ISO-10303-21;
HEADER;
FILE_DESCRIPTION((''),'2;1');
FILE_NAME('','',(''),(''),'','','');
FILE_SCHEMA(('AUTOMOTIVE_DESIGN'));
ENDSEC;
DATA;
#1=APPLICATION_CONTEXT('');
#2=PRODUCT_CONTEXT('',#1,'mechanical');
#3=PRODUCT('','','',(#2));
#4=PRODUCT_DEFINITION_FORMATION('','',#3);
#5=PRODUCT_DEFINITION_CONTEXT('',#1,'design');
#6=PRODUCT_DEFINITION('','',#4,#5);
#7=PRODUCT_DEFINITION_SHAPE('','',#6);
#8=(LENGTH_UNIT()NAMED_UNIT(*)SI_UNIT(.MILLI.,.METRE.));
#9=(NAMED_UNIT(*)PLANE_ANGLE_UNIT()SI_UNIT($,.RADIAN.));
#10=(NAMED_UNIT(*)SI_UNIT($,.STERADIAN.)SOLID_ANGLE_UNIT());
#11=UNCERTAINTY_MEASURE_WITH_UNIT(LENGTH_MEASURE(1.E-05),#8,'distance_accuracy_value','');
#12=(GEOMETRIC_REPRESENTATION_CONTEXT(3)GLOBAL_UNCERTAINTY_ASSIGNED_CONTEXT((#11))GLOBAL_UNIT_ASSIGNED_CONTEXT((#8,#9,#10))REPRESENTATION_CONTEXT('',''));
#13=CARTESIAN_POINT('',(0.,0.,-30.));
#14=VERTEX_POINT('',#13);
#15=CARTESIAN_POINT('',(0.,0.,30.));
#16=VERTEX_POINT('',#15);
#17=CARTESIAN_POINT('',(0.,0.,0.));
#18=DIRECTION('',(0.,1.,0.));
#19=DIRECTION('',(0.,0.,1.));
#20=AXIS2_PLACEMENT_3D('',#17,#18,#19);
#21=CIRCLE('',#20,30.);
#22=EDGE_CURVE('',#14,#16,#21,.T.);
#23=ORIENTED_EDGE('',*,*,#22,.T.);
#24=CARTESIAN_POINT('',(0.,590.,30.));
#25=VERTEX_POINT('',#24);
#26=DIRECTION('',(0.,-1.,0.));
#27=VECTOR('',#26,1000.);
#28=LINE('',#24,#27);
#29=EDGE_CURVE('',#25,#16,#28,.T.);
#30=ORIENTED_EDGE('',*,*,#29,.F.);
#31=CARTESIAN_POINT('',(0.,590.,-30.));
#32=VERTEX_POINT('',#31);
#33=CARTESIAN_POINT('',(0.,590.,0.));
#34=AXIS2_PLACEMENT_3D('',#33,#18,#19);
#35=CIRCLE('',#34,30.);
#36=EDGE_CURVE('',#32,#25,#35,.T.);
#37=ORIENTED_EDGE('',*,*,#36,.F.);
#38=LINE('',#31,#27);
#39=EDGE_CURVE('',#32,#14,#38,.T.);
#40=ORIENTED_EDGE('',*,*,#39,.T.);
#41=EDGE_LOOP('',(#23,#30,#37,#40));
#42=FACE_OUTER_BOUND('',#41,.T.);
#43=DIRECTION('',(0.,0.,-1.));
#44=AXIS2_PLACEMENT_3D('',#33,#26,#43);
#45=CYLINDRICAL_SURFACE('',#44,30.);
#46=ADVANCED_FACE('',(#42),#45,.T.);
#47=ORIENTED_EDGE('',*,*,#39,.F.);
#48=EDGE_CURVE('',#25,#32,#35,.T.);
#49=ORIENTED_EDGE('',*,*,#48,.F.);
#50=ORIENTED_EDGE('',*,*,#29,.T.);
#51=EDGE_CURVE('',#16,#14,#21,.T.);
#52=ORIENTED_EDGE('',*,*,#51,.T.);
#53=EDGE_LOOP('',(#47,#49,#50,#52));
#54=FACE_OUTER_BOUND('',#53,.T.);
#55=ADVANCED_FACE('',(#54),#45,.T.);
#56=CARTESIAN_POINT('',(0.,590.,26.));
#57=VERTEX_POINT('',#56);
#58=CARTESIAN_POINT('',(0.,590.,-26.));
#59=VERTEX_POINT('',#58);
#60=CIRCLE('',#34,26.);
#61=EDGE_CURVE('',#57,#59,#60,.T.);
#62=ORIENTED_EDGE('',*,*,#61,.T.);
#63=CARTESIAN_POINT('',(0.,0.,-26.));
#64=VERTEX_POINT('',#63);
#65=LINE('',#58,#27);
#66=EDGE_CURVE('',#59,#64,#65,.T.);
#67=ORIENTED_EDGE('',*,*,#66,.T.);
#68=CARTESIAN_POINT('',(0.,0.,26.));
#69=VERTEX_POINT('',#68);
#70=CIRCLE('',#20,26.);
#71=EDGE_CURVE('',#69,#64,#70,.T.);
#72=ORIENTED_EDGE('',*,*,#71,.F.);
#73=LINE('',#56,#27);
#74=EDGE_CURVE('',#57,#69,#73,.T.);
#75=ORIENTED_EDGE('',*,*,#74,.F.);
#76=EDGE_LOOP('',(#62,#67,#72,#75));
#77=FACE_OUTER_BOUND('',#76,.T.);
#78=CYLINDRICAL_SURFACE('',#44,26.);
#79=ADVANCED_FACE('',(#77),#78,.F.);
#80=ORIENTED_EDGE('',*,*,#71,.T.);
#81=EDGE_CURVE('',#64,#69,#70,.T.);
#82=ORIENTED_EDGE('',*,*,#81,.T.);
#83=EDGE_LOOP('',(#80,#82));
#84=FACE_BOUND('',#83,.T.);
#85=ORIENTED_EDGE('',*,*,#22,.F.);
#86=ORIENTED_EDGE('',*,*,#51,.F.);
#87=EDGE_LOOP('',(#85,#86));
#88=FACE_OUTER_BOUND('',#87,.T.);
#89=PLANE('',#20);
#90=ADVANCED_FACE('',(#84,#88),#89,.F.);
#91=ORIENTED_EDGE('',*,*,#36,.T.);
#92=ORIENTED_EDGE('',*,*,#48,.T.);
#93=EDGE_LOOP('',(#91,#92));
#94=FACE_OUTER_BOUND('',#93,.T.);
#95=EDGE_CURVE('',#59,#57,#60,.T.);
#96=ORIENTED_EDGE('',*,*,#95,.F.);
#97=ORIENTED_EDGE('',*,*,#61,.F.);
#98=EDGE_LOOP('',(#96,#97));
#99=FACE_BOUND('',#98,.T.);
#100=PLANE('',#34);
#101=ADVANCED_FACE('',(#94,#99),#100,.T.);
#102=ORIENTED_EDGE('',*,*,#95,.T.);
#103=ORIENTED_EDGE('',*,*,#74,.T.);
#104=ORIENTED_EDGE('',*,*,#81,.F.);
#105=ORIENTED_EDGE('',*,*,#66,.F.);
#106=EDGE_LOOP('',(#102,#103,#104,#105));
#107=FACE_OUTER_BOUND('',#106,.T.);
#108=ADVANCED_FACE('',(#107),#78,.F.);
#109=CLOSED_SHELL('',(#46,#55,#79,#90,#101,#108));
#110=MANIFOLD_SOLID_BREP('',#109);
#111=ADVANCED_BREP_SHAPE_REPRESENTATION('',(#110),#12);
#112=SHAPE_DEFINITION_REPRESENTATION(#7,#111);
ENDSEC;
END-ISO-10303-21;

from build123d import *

# Parameters (mm, degrees)
SKETCH11_R                             = 30
SKETCH11_R_2                           = 26
GB_T_6728_2002_ROUND_TUBE_60_4_1_DEPTH = 590


with BuildPart() as part:
    # Sketch11 → Gb/t 6728-2002 round tube 60 × 4(1) (new body)
    with BuildSketch(Plane(origin=(0, 0, 0), x_dir=(-1, 0, 0), z_dir=(0, 1, 0))):
        Circle(SKETCH11_R)
        Circle(SKETCH11_R_2, mode=Mode.SUBTRACT)
    extrude(amount=GB_T_6728_2002_ROUND_TUBE_60_4_1_DEPTH)


solid = part.part
